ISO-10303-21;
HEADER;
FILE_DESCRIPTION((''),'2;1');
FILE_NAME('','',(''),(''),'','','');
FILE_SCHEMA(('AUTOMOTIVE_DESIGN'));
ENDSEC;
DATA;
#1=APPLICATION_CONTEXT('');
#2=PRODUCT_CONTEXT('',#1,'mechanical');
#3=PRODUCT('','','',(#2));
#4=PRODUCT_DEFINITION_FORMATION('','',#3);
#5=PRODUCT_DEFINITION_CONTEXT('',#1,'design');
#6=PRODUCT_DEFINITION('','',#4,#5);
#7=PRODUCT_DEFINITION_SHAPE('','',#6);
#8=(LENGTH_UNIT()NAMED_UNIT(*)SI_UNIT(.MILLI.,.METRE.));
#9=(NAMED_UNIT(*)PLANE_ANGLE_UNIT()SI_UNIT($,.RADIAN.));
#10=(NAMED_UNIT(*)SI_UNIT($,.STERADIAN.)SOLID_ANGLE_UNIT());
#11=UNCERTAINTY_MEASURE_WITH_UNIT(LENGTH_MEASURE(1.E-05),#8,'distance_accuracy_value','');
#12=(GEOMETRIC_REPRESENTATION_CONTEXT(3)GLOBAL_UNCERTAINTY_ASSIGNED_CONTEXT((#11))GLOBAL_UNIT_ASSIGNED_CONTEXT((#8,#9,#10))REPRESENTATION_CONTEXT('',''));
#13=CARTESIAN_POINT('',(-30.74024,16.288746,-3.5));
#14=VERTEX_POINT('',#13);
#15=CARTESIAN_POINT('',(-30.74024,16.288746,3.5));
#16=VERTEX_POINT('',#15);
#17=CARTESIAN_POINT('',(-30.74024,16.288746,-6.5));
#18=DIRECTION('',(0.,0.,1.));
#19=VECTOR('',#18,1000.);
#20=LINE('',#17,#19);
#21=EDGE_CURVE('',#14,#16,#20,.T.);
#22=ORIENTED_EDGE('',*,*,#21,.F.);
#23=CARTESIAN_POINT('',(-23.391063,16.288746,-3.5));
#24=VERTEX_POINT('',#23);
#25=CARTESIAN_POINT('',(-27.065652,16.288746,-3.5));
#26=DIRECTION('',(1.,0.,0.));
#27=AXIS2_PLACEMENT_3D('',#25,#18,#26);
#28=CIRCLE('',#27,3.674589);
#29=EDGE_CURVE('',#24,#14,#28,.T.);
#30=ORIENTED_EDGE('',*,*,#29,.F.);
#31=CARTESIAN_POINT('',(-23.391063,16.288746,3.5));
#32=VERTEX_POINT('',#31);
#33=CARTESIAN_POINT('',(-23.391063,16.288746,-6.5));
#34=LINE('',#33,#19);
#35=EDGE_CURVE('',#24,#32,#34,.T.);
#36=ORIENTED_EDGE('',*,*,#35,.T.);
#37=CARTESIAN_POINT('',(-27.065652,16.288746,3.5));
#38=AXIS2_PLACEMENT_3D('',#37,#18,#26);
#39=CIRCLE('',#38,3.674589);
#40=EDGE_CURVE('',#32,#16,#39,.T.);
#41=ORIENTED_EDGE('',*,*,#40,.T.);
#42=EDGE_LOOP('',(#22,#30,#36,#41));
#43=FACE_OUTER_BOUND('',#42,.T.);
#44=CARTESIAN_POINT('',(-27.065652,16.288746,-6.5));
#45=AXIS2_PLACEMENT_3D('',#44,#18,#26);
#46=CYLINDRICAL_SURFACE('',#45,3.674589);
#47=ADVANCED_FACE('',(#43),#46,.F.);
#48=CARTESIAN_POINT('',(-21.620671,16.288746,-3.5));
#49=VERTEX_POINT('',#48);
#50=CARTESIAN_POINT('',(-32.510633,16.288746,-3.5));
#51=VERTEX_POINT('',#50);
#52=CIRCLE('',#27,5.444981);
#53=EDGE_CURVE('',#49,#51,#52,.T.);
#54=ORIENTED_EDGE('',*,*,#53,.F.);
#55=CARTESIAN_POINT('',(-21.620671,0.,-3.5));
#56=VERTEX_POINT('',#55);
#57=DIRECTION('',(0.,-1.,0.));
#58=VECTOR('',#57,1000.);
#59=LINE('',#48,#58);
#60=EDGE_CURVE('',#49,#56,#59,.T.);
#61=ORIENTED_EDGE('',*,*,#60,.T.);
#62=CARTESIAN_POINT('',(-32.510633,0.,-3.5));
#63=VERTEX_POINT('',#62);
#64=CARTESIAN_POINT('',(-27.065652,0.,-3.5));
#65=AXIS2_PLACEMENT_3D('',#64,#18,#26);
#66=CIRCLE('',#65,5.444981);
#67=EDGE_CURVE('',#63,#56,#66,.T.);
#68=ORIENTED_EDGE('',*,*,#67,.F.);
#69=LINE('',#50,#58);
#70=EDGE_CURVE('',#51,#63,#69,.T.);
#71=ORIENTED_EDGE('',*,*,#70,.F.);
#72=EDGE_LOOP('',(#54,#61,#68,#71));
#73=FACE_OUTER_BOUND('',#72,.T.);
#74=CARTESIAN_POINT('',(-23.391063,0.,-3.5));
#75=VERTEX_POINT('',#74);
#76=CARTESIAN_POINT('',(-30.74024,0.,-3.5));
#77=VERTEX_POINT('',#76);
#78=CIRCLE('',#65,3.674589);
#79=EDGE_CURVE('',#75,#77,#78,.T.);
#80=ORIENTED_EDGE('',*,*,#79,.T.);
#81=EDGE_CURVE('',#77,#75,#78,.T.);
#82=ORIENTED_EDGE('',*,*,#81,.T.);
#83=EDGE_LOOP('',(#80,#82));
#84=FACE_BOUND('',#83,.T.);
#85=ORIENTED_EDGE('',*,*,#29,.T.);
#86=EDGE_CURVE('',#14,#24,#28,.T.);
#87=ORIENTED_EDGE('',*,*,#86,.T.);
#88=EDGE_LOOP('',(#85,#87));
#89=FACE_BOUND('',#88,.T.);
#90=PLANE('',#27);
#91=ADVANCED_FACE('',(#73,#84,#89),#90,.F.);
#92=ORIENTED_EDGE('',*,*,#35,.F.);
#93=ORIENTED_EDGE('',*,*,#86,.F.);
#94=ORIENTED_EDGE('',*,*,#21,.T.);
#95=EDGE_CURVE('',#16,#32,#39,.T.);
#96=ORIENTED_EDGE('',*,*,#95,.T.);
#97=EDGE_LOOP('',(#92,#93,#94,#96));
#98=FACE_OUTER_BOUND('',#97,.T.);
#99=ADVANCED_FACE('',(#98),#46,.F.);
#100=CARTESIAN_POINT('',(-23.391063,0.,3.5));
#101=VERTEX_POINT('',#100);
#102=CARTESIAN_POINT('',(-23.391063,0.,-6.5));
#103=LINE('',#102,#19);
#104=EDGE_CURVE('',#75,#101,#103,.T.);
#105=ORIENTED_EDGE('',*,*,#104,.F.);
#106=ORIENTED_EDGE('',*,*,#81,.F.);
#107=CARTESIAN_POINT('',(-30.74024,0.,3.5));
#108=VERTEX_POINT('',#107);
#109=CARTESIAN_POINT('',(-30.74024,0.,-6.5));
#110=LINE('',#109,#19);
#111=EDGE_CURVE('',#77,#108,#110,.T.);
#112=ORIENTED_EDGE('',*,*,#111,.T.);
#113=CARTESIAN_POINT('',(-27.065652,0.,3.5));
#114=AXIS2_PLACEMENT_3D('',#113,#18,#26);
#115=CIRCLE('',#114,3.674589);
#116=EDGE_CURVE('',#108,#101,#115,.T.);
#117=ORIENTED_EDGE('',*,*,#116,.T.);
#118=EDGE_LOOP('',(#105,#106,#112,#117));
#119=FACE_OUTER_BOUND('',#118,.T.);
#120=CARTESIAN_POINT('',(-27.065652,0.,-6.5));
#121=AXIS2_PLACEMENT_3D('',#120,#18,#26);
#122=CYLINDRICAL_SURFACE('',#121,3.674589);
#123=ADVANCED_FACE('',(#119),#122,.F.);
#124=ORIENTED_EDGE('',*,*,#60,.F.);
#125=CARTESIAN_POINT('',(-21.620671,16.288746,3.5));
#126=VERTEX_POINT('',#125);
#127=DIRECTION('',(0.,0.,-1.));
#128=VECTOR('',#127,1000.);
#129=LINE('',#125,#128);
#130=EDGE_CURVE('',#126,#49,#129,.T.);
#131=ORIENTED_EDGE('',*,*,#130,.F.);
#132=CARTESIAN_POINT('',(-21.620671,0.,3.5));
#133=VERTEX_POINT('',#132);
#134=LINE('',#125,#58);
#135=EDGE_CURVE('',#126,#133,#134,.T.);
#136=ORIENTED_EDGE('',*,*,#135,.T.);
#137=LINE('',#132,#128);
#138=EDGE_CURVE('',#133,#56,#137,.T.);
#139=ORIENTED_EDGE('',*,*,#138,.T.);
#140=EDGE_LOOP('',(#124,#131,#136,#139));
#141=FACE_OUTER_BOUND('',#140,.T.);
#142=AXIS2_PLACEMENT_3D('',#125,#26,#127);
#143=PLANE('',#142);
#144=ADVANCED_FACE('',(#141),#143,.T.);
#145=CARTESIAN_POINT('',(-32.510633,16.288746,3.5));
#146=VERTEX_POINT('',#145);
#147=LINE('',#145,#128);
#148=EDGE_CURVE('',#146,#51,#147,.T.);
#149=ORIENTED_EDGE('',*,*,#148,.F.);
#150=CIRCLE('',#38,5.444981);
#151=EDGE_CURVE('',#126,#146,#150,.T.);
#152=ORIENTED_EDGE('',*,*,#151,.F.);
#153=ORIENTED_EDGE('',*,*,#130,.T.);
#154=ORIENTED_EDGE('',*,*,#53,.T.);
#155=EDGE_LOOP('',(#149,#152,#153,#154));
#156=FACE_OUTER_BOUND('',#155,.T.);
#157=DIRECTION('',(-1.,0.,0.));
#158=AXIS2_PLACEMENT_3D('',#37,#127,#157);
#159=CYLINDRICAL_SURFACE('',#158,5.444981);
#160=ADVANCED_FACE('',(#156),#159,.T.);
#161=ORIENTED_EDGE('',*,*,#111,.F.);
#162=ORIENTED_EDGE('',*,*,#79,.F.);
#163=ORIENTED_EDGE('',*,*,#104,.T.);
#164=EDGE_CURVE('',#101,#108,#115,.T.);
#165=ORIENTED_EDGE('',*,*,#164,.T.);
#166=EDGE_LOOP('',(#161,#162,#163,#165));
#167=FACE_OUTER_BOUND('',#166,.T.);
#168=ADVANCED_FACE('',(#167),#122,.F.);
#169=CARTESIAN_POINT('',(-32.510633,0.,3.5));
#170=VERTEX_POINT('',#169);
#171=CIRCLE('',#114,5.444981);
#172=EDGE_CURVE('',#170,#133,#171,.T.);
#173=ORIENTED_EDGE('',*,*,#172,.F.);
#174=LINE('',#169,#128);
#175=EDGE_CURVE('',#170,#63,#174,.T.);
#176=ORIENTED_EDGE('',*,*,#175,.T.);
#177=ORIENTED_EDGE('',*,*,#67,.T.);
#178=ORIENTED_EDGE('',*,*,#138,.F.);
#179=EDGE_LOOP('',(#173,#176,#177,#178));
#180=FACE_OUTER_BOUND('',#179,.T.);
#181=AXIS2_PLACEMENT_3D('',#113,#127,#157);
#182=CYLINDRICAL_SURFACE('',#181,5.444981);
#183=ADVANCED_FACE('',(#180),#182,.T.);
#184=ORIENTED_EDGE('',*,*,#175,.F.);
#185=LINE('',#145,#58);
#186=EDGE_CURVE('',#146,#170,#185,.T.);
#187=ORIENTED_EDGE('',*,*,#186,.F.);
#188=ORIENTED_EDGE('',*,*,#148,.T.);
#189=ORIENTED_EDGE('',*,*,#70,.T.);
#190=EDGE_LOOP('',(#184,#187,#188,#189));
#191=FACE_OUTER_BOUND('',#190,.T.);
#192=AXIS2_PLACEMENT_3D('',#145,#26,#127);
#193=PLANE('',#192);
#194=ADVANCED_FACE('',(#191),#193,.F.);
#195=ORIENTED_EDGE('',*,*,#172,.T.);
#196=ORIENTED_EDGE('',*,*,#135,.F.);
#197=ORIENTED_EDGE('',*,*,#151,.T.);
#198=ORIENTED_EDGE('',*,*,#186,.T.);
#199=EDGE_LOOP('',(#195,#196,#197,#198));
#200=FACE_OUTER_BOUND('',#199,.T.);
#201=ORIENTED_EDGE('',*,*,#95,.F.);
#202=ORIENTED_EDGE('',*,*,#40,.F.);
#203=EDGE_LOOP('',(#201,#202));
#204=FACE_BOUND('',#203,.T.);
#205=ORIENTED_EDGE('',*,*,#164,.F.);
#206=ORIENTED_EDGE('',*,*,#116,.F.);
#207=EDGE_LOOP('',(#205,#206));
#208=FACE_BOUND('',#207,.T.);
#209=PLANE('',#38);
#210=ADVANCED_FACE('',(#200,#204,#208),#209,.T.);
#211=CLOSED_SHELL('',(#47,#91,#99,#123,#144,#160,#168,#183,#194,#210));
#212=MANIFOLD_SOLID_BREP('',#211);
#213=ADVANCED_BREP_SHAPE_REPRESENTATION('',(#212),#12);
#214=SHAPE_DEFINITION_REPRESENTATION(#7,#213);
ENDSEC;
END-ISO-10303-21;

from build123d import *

# Parameters (mm, degrees)
BOSS_EXTRUDE2_DEPTH = 3.5
SKETCH4_R           = 3.674588618
CUT_EXTRUDE1_DEPTH  = 10
SKETCH2_R           = 3.674588618
CUT_EXTRUDE2_DEPTH  = 10


with BuildPart() as part:
    # Sketch1 → Boss-Extrude2 (new, symmetric)
    with BuildSketch(Plane.XY):
        with BuildLine():
            Line((-32.510632707, 16.288746435), (-32.510632707, 0))
            ThreePointArc((-32.510632707, 0), (-27.065651732, -5.444980975), (-21.620670757, 0))
            Line((-21.620670757, 0), (-21.620670757, 16.288746435))
            ThreePointArc((-21.620670757, 16.288746435), (-27.065651732, 21.73372741), (-32.510632707, 16.288746435))
        make_face()
    extrude(amount=BOSS_EXTRUDE2_DEPTH, both=True)

    # Sketch4 → Cut-Extrude1 (cut)
    with BuildSketch(Plane.XY.offset(3.5)):
        with Locations((-27.065651732, 0)):
            Circle(SKETCH4_R)
    extrude(amount=-CUT_EXTRUDE1_DEPTH, mode=Mode.SUBTRACT)

    # Sketch2 → Cut-Extrude2 (cut)
    with BuildSketch(Plane.XY.offset(3.5)):
        with Locations((-27.065651732, 16.288746435)):
            Circle(SKETCH2_R)
    extrude(amount=-CUT_EXTRUDE2_DEPTH, mode=Mode.SUBTRACT)


solid = part.part
